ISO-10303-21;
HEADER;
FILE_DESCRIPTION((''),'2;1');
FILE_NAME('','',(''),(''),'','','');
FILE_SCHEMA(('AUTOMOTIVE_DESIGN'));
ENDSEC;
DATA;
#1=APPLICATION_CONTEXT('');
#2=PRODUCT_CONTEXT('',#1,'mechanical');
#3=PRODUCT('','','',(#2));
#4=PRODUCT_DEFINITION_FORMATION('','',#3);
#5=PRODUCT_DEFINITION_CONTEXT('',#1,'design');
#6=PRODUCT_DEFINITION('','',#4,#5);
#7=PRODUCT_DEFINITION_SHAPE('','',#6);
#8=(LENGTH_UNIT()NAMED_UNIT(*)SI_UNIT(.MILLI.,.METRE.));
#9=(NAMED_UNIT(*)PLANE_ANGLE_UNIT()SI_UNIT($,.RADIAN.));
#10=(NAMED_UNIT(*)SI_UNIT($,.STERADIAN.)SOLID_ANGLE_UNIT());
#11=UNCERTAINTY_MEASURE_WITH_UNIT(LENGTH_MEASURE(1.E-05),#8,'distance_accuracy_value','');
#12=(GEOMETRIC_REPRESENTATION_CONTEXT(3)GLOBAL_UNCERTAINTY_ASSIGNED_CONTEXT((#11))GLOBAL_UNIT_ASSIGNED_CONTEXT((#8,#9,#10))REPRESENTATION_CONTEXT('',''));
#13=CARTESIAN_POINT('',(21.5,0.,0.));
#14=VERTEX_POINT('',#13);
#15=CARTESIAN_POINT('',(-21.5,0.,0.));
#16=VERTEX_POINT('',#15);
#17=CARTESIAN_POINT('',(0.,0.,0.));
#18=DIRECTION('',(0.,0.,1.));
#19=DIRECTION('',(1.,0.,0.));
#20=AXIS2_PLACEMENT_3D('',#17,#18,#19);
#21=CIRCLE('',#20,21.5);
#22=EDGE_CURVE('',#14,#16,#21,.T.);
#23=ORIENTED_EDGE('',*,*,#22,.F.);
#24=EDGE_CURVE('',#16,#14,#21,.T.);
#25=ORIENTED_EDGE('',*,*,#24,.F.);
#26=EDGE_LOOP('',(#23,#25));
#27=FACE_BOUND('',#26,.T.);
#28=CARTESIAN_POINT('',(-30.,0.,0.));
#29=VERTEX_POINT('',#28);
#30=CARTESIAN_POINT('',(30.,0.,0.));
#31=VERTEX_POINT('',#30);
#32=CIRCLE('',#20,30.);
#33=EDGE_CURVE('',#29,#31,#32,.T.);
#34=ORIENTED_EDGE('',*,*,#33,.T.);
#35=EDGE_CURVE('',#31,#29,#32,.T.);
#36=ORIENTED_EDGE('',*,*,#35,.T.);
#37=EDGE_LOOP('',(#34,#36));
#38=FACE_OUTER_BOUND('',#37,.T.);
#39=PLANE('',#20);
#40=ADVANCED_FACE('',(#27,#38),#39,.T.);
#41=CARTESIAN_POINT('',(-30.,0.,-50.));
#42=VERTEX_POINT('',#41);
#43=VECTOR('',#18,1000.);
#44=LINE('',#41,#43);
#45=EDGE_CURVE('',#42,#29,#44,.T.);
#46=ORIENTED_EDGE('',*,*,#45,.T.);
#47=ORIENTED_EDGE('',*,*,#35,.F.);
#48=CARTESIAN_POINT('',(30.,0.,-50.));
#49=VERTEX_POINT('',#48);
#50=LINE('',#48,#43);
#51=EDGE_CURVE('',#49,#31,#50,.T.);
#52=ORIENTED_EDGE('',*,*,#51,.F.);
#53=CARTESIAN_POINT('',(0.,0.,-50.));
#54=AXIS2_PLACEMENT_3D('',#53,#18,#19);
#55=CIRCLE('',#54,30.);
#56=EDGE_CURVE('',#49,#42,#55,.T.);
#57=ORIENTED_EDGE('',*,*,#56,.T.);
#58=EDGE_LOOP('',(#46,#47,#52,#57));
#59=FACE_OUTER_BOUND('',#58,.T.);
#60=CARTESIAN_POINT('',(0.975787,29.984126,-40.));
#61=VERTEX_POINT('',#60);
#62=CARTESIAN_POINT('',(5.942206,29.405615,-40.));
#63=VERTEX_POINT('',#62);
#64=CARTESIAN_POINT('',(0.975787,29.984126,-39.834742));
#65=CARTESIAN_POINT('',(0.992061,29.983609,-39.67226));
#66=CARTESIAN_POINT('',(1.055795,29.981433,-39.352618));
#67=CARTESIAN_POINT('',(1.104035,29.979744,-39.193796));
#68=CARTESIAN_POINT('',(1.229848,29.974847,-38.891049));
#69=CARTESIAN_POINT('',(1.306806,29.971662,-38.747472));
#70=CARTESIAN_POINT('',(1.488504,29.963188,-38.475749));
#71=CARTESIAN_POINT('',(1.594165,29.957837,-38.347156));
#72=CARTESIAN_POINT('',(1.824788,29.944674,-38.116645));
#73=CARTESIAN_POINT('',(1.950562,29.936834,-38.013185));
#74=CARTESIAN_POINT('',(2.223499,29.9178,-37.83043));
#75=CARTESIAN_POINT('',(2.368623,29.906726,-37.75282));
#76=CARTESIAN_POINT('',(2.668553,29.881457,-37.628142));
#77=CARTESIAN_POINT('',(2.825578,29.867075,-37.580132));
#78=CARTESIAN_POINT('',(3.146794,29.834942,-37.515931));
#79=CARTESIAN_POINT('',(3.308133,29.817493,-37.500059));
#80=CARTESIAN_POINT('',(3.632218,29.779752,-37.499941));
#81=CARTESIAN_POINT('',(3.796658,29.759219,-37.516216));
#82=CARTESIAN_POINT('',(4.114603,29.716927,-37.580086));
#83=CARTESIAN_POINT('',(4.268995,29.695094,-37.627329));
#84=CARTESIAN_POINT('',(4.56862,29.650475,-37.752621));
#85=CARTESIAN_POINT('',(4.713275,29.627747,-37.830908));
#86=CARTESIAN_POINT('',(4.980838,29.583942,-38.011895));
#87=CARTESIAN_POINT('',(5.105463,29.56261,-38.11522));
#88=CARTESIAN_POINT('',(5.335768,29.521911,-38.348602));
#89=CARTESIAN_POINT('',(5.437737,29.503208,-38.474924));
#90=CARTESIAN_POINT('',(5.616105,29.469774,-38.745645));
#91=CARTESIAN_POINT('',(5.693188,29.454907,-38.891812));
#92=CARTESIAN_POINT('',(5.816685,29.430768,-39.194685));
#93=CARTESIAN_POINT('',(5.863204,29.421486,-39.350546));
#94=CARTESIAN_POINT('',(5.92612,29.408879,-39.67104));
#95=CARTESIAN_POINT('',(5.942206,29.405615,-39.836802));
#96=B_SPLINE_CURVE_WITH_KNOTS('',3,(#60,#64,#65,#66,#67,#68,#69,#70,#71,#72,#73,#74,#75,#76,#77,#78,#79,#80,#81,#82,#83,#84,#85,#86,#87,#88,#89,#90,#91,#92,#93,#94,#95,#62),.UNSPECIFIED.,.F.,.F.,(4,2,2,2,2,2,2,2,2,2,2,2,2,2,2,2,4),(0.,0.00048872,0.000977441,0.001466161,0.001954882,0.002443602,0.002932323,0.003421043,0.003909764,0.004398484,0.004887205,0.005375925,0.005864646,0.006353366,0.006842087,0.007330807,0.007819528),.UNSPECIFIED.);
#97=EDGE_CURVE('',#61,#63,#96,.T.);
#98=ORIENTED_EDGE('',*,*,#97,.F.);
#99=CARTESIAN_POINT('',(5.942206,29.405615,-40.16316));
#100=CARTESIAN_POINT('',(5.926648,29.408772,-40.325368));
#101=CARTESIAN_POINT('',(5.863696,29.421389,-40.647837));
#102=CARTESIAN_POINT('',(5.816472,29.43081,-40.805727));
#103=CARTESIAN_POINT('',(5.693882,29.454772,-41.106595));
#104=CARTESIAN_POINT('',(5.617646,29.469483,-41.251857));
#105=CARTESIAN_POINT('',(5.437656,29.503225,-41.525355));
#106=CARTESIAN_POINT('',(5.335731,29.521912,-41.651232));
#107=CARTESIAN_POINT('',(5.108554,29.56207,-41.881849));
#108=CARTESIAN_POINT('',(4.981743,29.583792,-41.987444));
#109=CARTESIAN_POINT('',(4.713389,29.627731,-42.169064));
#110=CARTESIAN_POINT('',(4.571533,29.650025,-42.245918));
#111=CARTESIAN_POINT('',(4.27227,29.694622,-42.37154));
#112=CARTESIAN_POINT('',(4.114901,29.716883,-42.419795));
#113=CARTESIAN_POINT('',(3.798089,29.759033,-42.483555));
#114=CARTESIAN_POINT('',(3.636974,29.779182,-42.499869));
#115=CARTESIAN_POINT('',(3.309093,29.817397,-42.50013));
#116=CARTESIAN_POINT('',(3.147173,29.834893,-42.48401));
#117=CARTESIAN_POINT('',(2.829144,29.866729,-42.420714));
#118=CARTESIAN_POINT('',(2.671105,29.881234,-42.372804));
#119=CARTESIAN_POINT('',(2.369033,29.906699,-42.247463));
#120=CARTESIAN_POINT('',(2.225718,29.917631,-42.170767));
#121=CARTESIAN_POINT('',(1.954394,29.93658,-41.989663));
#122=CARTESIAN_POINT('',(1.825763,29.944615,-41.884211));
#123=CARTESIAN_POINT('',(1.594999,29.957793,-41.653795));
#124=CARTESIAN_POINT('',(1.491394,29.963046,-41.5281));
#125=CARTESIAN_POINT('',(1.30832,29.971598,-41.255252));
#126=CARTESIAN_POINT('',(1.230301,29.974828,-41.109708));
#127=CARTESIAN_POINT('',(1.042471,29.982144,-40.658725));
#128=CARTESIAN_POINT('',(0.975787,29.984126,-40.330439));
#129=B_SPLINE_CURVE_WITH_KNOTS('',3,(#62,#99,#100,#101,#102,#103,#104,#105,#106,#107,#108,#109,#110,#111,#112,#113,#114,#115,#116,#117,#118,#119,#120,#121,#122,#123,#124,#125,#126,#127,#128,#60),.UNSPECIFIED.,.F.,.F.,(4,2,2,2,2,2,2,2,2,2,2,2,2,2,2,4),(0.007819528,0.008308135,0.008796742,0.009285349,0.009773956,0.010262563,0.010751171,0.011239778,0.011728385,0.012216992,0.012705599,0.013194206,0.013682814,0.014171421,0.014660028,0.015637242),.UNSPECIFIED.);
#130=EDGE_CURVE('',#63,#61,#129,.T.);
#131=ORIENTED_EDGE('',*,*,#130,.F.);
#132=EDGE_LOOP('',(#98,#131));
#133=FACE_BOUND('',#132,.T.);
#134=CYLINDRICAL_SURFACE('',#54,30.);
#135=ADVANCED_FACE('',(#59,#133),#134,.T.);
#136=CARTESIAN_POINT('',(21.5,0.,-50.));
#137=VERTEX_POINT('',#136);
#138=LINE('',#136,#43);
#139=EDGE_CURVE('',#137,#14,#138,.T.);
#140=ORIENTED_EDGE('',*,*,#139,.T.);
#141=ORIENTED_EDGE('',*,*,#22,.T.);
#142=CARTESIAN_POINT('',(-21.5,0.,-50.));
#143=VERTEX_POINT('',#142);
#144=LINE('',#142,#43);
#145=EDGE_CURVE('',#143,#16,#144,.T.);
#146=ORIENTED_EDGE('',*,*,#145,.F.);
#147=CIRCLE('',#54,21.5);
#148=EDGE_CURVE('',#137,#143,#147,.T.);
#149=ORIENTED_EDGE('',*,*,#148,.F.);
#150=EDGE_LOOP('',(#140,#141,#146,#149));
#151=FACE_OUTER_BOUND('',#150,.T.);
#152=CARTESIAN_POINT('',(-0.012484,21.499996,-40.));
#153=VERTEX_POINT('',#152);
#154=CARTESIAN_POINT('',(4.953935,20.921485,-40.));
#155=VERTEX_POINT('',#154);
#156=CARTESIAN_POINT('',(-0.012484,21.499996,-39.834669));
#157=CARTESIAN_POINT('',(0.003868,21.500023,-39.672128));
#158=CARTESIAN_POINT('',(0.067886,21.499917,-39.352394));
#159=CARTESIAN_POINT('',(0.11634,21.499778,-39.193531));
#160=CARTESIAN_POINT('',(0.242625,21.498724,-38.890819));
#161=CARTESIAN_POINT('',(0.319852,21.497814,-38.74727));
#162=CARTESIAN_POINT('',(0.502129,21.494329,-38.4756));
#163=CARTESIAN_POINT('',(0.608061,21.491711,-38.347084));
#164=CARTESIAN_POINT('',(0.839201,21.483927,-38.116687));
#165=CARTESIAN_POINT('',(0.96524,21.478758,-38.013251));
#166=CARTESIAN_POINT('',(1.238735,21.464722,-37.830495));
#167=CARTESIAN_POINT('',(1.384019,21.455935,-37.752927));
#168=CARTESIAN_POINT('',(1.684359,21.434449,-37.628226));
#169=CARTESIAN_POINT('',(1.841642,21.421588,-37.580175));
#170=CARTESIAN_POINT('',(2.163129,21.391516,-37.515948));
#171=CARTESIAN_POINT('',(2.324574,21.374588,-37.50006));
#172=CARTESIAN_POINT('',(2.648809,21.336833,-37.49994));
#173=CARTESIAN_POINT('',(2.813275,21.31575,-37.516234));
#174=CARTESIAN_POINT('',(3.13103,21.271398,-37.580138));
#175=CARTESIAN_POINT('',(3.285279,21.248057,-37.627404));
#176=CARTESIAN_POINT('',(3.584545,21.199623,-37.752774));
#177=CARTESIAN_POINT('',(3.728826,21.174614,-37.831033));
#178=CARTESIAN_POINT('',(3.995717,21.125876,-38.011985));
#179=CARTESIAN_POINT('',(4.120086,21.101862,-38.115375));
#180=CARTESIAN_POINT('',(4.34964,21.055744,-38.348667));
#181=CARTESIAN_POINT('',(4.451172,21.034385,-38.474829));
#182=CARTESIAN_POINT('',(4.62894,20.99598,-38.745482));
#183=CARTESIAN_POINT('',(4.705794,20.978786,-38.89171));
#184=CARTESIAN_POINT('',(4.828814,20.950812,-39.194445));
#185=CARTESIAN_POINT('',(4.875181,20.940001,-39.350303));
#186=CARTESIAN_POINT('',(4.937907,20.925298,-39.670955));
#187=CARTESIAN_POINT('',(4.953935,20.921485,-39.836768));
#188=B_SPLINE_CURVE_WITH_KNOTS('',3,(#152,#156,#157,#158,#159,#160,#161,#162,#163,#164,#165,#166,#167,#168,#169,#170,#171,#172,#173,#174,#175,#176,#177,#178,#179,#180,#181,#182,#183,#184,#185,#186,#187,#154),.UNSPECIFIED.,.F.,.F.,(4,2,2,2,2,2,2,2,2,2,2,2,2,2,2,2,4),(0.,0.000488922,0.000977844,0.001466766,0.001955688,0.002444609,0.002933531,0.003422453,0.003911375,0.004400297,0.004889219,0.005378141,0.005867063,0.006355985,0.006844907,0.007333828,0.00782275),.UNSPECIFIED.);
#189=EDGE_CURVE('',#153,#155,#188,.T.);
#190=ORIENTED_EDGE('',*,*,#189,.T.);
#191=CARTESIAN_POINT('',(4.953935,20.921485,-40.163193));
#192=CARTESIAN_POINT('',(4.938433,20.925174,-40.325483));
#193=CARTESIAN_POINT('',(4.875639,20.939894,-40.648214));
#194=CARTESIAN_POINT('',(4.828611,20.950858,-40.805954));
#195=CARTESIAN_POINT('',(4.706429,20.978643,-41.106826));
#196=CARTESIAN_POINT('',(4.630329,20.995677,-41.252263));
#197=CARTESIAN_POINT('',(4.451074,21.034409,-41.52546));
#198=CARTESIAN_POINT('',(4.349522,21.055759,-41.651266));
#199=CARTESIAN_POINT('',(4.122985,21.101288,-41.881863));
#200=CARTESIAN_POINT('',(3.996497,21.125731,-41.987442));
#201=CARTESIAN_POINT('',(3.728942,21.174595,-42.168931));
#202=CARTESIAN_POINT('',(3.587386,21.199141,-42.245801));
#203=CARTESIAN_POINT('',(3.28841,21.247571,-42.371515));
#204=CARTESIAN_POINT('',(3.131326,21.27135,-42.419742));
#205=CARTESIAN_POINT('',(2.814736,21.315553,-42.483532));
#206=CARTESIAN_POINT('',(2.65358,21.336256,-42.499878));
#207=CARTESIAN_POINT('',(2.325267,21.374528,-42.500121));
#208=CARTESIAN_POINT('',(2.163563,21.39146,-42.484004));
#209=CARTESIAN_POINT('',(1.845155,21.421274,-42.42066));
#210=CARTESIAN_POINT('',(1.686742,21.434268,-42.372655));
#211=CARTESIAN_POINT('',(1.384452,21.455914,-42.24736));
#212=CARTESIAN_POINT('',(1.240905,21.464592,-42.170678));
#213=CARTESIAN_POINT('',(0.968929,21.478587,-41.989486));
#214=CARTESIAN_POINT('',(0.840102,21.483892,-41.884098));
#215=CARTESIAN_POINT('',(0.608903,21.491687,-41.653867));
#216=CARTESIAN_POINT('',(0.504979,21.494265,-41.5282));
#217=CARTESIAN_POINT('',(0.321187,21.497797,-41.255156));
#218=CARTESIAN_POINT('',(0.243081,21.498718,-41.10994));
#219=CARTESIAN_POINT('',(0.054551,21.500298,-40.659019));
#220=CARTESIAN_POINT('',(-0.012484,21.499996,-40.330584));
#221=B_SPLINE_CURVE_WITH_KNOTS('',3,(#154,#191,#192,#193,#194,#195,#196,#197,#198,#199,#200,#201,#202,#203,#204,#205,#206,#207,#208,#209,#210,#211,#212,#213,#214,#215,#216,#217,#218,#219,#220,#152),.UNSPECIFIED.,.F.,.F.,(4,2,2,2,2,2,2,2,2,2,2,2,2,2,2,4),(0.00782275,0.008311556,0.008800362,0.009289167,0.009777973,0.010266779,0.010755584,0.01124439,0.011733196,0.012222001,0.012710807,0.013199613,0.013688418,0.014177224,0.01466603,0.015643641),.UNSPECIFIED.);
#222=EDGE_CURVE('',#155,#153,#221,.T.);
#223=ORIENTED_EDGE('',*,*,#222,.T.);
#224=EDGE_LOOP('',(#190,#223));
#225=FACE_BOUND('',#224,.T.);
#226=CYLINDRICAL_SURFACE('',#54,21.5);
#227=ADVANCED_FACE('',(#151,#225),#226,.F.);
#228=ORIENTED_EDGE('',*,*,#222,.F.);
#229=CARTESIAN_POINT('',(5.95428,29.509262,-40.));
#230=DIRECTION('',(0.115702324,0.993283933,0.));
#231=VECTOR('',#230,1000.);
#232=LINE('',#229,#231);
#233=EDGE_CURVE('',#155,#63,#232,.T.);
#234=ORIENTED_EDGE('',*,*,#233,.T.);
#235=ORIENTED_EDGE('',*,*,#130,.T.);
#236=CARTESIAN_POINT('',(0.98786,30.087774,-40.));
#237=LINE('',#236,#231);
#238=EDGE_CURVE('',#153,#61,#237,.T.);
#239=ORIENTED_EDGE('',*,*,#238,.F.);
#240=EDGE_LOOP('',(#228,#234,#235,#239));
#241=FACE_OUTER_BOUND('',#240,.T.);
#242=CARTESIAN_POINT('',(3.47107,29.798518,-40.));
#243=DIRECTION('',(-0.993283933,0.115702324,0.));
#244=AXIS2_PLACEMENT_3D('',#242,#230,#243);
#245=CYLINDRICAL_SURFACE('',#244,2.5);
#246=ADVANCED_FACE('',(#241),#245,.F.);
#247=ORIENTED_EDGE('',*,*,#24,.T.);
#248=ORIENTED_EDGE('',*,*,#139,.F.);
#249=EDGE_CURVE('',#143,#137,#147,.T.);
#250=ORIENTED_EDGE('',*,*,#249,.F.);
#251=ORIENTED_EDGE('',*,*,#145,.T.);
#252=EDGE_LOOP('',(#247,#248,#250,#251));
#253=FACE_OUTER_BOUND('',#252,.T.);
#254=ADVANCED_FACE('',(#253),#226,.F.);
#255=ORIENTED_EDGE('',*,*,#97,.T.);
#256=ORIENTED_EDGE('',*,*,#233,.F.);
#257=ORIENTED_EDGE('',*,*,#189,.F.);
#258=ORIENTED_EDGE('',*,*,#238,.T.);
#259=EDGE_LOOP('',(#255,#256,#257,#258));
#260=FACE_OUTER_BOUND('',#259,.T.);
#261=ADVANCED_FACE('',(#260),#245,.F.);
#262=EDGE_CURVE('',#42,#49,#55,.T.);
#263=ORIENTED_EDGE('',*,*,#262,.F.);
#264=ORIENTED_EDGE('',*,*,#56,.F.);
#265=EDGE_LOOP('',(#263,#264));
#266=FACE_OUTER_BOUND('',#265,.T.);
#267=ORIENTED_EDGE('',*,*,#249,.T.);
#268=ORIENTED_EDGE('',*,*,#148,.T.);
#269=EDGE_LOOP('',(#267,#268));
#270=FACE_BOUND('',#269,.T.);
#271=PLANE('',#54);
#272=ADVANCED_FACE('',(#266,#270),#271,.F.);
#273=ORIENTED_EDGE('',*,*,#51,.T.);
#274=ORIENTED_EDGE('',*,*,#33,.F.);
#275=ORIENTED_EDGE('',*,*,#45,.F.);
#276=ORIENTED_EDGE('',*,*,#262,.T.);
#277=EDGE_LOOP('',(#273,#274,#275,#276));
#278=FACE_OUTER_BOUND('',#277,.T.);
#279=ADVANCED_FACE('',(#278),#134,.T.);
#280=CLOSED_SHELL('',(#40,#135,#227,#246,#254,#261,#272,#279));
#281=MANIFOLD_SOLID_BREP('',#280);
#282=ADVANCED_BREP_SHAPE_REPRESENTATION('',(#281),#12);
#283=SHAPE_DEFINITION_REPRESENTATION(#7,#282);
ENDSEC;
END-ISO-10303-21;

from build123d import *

# Parameters (mm, degrees)
SKETCH1_R             = 30
SKETCH1_R_2           = 21.5
BOSS_EXTRUDE1_DEPTH   = 50
M6_TAPPED_HOLE1_D     = 5
M6_TAPPED_HOLE1_DEPTH = 18
M6_TAPPED_HOLE1_TIP   = 1.502151548
BOSS_EXTRUDE2_START   = 24
SKETCH4_R             = 25
SKETCH4_R_2           = 21.5
BOSS_EXTRUDE2_DEPTH   = 24
SKETCH6_R             = 25
SKETCH6_R_2           = 21.5
CUT_EXTRUDE1_DEPTH    = 24


with BuildPart() as part:
    # Sketch1 → Boss-Extrude1 (new body)
    with BuildSketch(Plane.XY):
        Circle(SKETCH1_R)
        Circle(SKETCH1_R_2, mode=Mode.SUBTRACT)
    extrude(amount=-BOSS_EXTRUDE1_DEPTH)

    # M6 Tapped Hole1
    with Locations(Plane(origin=(3.471069712, 29.798518001, -40), x_dir=(0.993283933364, -0.115702323745, 0), z_dir=(0.115702323745, 0.993283933364, 0))):
        with Locations((0, 0)):
            Hole(M6_TAPPED_HOLE1_D / 2, depth=M6_TAPPED_HOLE1_DEPTH)
            with Locations((0, 0, -(M6_TAPPED_HOLE1_DEPTH + M6_TAPPED_HOLE1_TIP / 2))):  # 118° drill point
                Cone(0, M6_TAPPED_HOLE1_D / 2, M6_TAPPED_HOLE1_TIP, mode=Mode.SUBTRACT)

    # Sketch4 → Boss-Extrude2 (add)
    with BuildSketch(Plane.XY.offset(BOSS_EXTRUDE2_START)):
        Circle(SKETCH4_R)
        Circle(SKETCH4_R_2, mode=Mode.SUBTRACT)
    extrude(amount=-BOSS_EXTRUDE2_DEPTH)

    # Sketch6 → Cut-Extrude1 (cut)
    with BuildSketch(Plane.XY.offset(24)):
        Circle(SKETCH6_R)
        Circle(SKETCH6_R_2, mode=Mode.SUBTRACT)
    extrude(amount=-CUT_EXTRUDE1_DEPTH, mode=Mode.SUBTRACT)


solid = part.part
